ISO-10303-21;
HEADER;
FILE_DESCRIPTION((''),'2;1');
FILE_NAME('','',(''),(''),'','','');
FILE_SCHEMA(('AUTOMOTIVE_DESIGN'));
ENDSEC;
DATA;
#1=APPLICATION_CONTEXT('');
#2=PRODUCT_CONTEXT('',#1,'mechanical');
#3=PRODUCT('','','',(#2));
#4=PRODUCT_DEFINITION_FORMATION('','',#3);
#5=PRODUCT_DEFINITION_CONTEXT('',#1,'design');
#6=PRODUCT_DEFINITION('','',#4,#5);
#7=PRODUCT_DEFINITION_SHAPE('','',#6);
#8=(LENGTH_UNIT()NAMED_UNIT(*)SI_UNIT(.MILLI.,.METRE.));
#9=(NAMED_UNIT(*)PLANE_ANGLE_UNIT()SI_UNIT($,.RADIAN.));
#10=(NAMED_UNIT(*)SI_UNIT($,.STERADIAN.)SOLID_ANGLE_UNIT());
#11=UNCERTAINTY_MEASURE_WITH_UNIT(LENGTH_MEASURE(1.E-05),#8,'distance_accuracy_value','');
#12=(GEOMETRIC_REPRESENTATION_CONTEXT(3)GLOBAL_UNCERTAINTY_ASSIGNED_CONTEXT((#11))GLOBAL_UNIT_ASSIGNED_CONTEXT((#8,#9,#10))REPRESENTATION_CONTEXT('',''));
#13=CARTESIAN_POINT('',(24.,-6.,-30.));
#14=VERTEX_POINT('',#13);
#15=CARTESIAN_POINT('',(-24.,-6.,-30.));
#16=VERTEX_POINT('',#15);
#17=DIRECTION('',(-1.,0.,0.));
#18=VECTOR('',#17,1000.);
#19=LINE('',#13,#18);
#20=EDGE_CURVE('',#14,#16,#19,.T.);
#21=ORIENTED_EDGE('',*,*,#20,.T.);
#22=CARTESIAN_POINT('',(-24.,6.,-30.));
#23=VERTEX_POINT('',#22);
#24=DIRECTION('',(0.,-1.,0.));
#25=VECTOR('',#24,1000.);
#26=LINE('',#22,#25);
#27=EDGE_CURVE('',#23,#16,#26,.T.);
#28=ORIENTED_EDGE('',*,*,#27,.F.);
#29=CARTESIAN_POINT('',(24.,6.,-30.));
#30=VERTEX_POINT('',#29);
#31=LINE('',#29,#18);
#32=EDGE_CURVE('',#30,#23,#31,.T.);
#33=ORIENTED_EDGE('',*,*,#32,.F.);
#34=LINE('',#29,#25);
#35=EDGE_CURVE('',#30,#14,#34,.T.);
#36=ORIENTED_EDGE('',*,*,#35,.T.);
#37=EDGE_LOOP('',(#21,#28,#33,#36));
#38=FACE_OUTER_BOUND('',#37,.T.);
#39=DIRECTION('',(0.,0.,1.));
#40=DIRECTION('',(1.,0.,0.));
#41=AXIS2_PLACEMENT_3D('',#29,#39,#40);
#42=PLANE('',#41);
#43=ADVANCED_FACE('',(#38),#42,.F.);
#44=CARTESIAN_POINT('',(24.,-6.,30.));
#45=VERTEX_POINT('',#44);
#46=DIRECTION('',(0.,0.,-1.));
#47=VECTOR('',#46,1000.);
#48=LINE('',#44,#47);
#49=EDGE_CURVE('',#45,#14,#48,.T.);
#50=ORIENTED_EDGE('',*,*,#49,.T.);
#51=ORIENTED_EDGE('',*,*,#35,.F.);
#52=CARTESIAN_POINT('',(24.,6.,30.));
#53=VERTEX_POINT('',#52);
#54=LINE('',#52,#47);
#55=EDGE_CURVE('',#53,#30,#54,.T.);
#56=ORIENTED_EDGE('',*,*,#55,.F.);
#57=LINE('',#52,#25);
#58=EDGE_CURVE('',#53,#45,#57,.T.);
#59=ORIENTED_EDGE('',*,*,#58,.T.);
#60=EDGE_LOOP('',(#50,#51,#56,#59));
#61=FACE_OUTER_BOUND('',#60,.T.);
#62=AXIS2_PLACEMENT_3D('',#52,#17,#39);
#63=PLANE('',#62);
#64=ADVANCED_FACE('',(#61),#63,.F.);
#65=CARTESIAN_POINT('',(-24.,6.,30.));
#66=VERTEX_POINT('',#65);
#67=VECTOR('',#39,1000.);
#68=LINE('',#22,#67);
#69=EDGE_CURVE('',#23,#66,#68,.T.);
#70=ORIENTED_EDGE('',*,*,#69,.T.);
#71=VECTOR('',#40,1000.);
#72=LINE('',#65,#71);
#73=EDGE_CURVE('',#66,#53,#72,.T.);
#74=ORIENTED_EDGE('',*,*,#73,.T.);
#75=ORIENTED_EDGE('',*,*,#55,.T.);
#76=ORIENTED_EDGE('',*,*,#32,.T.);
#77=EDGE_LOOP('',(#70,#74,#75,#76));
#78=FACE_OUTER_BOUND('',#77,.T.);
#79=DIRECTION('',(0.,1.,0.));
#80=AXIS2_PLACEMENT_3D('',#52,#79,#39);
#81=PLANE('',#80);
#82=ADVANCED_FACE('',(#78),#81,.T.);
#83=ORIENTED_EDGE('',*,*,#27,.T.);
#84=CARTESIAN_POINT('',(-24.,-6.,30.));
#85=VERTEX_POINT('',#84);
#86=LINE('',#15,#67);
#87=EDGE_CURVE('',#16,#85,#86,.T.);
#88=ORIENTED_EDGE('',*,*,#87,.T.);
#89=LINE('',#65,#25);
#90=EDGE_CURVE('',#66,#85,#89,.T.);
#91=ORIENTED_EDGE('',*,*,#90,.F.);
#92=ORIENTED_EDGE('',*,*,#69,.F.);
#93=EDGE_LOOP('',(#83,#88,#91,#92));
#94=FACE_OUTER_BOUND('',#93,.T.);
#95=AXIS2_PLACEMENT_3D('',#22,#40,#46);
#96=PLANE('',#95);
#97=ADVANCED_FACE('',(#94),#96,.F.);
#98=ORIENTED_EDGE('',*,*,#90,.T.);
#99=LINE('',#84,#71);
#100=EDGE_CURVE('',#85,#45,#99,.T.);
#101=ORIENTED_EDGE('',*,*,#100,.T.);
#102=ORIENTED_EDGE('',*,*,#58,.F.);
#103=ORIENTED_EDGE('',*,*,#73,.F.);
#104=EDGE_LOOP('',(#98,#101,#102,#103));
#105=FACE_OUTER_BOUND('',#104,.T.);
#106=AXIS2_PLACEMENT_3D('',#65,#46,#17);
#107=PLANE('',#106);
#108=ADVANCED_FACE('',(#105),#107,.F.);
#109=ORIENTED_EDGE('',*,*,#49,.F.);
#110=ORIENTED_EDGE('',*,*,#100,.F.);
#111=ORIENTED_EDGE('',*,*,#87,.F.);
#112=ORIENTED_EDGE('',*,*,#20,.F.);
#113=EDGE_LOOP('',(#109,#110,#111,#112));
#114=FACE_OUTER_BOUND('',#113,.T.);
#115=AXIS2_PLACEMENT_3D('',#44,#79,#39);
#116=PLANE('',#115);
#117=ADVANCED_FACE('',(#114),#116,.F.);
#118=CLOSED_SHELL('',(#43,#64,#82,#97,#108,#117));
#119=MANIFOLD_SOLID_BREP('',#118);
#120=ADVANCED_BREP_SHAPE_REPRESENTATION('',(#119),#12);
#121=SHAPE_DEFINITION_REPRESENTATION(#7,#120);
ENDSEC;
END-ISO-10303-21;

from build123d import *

# Parameters (mm, degrees)
SKETCH1_W      = 48
SKETCH1_H      = 60
EXTRUDE1_DEPTH = 6


with BuildPart() as part:
    # Sketch1 → Extrude1 (new, symmetric)
    with BuildSketch(Plane(origin=(0, 0, 0), x_dir=(1, 0, 0), z_dir=(0, 1, 0))):
        Rectangle(SKETCH1_W, SKETCH1_H)
    extrude(amount=EXTRUDE1_DEPTH, both=True)


solid = part.part
